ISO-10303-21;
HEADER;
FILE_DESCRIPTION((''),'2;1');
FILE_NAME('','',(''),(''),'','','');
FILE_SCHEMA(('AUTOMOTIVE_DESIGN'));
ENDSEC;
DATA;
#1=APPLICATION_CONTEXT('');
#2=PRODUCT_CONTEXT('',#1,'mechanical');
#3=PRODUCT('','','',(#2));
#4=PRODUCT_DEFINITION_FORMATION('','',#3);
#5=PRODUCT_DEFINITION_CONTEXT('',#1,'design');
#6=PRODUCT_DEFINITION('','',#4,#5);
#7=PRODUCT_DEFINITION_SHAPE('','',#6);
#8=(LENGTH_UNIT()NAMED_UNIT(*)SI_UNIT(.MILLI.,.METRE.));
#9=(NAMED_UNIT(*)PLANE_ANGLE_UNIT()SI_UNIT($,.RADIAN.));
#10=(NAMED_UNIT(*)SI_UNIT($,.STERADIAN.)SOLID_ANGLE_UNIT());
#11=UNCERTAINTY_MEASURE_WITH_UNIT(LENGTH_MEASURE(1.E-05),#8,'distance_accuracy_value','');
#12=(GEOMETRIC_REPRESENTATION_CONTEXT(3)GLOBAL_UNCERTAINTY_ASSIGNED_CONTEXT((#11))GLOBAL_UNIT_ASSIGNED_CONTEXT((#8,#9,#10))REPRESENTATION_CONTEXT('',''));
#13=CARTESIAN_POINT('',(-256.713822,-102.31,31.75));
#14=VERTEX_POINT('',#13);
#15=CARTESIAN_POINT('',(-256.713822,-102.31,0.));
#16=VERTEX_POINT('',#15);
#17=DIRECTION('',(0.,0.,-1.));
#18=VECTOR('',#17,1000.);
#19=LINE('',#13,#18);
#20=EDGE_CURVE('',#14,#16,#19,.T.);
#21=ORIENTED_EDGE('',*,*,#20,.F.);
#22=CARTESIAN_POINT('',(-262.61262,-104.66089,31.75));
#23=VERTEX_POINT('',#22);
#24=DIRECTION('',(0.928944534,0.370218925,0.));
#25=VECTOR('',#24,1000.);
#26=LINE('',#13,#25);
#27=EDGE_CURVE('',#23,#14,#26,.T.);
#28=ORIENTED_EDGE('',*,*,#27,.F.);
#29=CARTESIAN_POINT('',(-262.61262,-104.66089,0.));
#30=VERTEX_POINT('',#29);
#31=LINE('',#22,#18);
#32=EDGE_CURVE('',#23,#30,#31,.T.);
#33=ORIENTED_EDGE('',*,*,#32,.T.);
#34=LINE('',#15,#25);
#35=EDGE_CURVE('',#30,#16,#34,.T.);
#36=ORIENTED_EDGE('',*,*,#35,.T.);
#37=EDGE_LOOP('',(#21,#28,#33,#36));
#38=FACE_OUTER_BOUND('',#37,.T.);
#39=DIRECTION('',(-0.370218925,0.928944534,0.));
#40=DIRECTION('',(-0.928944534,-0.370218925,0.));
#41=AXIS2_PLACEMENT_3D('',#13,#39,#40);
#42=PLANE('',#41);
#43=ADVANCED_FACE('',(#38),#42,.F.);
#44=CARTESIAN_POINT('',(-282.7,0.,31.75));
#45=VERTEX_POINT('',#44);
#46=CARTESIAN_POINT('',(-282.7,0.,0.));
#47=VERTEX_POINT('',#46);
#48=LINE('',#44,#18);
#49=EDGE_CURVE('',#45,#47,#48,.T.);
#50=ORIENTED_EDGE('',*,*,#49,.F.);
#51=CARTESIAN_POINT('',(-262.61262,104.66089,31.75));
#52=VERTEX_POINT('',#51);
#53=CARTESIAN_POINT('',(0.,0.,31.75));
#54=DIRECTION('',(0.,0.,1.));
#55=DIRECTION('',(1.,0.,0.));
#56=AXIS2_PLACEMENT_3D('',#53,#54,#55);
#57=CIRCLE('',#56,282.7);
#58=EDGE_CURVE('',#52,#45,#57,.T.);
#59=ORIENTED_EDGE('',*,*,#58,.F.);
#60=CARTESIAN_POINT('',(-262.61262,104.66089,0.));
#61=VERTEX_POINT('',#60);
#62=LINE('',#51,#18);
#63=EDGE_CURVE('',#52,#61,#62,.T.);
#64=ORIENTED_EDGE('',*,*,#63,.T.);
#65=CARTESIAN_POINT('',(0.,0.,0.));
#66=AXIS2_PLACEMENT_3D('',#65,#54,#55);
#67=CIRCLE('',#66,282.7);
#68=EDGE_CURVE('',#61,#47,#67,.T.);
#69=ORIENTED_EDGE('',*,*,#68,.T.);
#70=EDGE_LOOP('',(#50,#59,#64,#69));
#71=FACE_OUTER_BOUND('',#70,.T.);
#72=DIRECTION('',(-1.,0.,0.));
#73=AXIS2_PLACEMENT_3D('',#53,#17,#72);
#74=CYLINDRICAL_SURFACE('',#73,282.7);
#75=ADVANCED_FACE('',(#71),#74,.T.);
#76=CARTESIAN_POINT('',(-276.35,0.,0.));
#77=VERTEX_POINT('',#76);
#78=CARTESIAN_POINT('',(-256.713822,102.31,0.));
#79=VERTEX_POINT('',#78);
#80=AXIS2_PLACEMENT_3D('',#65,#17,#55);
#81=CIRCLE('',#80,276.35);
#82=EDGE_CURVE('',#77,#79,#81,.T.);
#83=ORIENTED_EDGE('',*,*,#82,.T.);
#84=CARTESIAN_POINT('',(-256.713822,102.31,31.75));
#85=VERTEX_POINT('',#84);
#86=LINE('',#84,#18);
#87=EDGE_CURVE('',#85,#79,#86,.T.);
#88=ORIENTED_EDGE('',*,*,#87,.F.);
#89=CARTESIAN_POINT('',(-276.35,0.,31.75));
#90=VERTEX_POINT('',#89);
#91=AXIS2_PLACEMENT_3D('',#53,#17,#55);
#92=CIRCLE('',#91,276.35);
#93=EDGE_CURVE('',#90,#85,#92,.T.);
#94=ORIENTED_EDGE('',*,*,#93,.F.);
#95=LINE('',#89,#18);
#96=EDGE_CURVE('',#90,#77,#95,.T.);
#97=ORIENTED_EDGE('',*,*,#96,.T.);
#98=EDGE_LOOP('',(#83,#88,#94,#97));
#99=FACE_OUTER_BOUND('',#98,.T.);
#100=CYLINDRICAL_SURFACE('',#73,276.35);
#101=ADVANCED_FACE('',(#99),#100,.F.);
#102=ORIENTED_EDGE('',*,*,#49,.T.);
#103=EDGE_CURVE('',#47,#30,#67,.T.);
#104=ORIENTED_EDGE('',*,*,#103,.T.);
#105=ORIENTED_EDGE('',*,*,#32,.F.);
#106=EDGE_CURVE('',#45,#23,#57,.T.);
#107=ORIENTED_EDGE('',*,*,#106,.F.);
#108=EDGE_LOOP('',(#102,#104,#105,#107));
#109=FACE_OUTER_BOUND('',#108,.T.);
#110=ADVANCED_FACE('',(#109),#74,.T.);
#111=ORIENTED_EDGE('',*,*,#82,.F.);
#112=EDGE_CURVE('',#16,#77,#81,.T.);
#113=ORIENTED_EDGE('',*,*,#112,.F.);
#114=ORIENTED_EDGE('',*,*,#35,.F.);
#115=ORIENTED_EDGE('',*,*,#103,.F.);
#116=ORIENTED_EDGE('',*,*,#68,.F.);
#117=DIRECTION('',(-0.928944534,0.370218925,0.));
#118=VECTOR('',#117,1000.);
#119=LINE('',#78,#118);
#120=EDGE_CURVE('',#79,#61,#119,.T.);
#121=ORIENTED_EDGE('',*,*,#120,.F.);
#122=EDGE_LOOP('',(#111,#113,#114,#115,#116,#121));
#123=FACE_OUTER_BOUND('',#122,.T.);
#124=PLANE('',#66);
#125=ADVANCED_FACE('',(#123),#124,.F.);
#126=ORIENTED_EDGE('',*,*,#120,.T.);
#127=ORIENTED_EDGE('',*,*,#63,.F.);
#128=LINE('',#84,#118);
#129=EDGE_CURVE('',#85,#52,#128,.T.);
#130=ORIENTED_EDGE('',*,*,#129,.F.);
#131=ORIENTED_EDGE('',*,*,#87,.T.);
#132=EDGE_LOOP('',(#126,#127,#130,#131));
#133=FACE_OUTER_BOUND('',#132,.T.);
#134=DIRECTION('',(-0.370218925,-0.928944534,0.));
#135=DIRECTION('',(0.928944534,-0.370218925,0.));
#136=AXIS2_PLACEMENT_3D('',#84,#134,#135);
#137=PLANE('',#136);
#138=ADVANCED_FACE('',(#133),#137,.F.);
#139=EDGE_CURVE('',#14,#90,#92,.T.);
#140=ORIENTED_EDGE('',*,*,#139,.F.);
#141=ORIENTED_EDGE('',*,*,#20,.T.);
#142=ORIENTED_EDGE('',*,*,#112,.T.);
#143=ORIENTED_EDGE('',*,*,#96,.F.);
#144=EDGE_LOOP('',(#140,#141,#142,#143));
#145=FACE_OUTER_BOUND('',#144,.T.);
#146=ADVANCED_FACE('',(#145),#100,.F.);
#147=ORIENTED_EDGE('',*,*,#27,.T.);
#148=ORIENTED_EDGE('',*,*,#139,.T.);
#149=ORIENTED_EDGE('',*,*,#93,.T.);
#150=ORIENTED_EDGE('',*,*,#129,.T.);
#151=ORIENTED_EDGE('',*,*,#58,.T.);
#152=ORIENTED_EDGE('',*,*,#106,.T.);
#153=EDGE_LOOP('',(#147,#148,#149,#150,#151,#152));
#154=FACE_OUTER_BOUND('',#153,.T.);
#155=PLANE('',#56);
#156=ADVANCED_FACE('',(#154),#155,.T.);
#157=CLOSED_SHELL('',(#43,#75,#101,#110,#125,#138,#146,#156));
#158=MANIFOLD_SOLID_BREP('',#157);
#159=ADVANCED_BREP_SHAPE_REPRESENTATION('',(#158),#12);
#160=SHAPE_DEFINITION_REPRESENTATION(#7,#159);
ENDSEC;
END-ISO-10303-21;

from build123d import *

# Parameters (mm, degrees)
BOSS_EXTRUDE1_DEPTH = 31.75


with BuildPart() as part:
    # Sketch1 → Boss-Extrude1 (new body)
    with BuildSketch(Plane.XY):
        with BuildLine():
            Line((-256.713821989, 102.31), (-262.61261978, 104.660890176))
            ThreePointArc((-262.61261978, 104.660890176), (-282.7, 0), (-262.61261978, -104.660890176))
            Line((-262.61261978, -104.660890176), (-256.713821989, -102.31))
            ThreePointArc((-256.713821989, -102.31), (-276.35, 0), (-256.713821989, 102.31))
        make_face()
    extrude(amount=BOSS_EXTRUDE1_DEPTH)


solid = part.part
